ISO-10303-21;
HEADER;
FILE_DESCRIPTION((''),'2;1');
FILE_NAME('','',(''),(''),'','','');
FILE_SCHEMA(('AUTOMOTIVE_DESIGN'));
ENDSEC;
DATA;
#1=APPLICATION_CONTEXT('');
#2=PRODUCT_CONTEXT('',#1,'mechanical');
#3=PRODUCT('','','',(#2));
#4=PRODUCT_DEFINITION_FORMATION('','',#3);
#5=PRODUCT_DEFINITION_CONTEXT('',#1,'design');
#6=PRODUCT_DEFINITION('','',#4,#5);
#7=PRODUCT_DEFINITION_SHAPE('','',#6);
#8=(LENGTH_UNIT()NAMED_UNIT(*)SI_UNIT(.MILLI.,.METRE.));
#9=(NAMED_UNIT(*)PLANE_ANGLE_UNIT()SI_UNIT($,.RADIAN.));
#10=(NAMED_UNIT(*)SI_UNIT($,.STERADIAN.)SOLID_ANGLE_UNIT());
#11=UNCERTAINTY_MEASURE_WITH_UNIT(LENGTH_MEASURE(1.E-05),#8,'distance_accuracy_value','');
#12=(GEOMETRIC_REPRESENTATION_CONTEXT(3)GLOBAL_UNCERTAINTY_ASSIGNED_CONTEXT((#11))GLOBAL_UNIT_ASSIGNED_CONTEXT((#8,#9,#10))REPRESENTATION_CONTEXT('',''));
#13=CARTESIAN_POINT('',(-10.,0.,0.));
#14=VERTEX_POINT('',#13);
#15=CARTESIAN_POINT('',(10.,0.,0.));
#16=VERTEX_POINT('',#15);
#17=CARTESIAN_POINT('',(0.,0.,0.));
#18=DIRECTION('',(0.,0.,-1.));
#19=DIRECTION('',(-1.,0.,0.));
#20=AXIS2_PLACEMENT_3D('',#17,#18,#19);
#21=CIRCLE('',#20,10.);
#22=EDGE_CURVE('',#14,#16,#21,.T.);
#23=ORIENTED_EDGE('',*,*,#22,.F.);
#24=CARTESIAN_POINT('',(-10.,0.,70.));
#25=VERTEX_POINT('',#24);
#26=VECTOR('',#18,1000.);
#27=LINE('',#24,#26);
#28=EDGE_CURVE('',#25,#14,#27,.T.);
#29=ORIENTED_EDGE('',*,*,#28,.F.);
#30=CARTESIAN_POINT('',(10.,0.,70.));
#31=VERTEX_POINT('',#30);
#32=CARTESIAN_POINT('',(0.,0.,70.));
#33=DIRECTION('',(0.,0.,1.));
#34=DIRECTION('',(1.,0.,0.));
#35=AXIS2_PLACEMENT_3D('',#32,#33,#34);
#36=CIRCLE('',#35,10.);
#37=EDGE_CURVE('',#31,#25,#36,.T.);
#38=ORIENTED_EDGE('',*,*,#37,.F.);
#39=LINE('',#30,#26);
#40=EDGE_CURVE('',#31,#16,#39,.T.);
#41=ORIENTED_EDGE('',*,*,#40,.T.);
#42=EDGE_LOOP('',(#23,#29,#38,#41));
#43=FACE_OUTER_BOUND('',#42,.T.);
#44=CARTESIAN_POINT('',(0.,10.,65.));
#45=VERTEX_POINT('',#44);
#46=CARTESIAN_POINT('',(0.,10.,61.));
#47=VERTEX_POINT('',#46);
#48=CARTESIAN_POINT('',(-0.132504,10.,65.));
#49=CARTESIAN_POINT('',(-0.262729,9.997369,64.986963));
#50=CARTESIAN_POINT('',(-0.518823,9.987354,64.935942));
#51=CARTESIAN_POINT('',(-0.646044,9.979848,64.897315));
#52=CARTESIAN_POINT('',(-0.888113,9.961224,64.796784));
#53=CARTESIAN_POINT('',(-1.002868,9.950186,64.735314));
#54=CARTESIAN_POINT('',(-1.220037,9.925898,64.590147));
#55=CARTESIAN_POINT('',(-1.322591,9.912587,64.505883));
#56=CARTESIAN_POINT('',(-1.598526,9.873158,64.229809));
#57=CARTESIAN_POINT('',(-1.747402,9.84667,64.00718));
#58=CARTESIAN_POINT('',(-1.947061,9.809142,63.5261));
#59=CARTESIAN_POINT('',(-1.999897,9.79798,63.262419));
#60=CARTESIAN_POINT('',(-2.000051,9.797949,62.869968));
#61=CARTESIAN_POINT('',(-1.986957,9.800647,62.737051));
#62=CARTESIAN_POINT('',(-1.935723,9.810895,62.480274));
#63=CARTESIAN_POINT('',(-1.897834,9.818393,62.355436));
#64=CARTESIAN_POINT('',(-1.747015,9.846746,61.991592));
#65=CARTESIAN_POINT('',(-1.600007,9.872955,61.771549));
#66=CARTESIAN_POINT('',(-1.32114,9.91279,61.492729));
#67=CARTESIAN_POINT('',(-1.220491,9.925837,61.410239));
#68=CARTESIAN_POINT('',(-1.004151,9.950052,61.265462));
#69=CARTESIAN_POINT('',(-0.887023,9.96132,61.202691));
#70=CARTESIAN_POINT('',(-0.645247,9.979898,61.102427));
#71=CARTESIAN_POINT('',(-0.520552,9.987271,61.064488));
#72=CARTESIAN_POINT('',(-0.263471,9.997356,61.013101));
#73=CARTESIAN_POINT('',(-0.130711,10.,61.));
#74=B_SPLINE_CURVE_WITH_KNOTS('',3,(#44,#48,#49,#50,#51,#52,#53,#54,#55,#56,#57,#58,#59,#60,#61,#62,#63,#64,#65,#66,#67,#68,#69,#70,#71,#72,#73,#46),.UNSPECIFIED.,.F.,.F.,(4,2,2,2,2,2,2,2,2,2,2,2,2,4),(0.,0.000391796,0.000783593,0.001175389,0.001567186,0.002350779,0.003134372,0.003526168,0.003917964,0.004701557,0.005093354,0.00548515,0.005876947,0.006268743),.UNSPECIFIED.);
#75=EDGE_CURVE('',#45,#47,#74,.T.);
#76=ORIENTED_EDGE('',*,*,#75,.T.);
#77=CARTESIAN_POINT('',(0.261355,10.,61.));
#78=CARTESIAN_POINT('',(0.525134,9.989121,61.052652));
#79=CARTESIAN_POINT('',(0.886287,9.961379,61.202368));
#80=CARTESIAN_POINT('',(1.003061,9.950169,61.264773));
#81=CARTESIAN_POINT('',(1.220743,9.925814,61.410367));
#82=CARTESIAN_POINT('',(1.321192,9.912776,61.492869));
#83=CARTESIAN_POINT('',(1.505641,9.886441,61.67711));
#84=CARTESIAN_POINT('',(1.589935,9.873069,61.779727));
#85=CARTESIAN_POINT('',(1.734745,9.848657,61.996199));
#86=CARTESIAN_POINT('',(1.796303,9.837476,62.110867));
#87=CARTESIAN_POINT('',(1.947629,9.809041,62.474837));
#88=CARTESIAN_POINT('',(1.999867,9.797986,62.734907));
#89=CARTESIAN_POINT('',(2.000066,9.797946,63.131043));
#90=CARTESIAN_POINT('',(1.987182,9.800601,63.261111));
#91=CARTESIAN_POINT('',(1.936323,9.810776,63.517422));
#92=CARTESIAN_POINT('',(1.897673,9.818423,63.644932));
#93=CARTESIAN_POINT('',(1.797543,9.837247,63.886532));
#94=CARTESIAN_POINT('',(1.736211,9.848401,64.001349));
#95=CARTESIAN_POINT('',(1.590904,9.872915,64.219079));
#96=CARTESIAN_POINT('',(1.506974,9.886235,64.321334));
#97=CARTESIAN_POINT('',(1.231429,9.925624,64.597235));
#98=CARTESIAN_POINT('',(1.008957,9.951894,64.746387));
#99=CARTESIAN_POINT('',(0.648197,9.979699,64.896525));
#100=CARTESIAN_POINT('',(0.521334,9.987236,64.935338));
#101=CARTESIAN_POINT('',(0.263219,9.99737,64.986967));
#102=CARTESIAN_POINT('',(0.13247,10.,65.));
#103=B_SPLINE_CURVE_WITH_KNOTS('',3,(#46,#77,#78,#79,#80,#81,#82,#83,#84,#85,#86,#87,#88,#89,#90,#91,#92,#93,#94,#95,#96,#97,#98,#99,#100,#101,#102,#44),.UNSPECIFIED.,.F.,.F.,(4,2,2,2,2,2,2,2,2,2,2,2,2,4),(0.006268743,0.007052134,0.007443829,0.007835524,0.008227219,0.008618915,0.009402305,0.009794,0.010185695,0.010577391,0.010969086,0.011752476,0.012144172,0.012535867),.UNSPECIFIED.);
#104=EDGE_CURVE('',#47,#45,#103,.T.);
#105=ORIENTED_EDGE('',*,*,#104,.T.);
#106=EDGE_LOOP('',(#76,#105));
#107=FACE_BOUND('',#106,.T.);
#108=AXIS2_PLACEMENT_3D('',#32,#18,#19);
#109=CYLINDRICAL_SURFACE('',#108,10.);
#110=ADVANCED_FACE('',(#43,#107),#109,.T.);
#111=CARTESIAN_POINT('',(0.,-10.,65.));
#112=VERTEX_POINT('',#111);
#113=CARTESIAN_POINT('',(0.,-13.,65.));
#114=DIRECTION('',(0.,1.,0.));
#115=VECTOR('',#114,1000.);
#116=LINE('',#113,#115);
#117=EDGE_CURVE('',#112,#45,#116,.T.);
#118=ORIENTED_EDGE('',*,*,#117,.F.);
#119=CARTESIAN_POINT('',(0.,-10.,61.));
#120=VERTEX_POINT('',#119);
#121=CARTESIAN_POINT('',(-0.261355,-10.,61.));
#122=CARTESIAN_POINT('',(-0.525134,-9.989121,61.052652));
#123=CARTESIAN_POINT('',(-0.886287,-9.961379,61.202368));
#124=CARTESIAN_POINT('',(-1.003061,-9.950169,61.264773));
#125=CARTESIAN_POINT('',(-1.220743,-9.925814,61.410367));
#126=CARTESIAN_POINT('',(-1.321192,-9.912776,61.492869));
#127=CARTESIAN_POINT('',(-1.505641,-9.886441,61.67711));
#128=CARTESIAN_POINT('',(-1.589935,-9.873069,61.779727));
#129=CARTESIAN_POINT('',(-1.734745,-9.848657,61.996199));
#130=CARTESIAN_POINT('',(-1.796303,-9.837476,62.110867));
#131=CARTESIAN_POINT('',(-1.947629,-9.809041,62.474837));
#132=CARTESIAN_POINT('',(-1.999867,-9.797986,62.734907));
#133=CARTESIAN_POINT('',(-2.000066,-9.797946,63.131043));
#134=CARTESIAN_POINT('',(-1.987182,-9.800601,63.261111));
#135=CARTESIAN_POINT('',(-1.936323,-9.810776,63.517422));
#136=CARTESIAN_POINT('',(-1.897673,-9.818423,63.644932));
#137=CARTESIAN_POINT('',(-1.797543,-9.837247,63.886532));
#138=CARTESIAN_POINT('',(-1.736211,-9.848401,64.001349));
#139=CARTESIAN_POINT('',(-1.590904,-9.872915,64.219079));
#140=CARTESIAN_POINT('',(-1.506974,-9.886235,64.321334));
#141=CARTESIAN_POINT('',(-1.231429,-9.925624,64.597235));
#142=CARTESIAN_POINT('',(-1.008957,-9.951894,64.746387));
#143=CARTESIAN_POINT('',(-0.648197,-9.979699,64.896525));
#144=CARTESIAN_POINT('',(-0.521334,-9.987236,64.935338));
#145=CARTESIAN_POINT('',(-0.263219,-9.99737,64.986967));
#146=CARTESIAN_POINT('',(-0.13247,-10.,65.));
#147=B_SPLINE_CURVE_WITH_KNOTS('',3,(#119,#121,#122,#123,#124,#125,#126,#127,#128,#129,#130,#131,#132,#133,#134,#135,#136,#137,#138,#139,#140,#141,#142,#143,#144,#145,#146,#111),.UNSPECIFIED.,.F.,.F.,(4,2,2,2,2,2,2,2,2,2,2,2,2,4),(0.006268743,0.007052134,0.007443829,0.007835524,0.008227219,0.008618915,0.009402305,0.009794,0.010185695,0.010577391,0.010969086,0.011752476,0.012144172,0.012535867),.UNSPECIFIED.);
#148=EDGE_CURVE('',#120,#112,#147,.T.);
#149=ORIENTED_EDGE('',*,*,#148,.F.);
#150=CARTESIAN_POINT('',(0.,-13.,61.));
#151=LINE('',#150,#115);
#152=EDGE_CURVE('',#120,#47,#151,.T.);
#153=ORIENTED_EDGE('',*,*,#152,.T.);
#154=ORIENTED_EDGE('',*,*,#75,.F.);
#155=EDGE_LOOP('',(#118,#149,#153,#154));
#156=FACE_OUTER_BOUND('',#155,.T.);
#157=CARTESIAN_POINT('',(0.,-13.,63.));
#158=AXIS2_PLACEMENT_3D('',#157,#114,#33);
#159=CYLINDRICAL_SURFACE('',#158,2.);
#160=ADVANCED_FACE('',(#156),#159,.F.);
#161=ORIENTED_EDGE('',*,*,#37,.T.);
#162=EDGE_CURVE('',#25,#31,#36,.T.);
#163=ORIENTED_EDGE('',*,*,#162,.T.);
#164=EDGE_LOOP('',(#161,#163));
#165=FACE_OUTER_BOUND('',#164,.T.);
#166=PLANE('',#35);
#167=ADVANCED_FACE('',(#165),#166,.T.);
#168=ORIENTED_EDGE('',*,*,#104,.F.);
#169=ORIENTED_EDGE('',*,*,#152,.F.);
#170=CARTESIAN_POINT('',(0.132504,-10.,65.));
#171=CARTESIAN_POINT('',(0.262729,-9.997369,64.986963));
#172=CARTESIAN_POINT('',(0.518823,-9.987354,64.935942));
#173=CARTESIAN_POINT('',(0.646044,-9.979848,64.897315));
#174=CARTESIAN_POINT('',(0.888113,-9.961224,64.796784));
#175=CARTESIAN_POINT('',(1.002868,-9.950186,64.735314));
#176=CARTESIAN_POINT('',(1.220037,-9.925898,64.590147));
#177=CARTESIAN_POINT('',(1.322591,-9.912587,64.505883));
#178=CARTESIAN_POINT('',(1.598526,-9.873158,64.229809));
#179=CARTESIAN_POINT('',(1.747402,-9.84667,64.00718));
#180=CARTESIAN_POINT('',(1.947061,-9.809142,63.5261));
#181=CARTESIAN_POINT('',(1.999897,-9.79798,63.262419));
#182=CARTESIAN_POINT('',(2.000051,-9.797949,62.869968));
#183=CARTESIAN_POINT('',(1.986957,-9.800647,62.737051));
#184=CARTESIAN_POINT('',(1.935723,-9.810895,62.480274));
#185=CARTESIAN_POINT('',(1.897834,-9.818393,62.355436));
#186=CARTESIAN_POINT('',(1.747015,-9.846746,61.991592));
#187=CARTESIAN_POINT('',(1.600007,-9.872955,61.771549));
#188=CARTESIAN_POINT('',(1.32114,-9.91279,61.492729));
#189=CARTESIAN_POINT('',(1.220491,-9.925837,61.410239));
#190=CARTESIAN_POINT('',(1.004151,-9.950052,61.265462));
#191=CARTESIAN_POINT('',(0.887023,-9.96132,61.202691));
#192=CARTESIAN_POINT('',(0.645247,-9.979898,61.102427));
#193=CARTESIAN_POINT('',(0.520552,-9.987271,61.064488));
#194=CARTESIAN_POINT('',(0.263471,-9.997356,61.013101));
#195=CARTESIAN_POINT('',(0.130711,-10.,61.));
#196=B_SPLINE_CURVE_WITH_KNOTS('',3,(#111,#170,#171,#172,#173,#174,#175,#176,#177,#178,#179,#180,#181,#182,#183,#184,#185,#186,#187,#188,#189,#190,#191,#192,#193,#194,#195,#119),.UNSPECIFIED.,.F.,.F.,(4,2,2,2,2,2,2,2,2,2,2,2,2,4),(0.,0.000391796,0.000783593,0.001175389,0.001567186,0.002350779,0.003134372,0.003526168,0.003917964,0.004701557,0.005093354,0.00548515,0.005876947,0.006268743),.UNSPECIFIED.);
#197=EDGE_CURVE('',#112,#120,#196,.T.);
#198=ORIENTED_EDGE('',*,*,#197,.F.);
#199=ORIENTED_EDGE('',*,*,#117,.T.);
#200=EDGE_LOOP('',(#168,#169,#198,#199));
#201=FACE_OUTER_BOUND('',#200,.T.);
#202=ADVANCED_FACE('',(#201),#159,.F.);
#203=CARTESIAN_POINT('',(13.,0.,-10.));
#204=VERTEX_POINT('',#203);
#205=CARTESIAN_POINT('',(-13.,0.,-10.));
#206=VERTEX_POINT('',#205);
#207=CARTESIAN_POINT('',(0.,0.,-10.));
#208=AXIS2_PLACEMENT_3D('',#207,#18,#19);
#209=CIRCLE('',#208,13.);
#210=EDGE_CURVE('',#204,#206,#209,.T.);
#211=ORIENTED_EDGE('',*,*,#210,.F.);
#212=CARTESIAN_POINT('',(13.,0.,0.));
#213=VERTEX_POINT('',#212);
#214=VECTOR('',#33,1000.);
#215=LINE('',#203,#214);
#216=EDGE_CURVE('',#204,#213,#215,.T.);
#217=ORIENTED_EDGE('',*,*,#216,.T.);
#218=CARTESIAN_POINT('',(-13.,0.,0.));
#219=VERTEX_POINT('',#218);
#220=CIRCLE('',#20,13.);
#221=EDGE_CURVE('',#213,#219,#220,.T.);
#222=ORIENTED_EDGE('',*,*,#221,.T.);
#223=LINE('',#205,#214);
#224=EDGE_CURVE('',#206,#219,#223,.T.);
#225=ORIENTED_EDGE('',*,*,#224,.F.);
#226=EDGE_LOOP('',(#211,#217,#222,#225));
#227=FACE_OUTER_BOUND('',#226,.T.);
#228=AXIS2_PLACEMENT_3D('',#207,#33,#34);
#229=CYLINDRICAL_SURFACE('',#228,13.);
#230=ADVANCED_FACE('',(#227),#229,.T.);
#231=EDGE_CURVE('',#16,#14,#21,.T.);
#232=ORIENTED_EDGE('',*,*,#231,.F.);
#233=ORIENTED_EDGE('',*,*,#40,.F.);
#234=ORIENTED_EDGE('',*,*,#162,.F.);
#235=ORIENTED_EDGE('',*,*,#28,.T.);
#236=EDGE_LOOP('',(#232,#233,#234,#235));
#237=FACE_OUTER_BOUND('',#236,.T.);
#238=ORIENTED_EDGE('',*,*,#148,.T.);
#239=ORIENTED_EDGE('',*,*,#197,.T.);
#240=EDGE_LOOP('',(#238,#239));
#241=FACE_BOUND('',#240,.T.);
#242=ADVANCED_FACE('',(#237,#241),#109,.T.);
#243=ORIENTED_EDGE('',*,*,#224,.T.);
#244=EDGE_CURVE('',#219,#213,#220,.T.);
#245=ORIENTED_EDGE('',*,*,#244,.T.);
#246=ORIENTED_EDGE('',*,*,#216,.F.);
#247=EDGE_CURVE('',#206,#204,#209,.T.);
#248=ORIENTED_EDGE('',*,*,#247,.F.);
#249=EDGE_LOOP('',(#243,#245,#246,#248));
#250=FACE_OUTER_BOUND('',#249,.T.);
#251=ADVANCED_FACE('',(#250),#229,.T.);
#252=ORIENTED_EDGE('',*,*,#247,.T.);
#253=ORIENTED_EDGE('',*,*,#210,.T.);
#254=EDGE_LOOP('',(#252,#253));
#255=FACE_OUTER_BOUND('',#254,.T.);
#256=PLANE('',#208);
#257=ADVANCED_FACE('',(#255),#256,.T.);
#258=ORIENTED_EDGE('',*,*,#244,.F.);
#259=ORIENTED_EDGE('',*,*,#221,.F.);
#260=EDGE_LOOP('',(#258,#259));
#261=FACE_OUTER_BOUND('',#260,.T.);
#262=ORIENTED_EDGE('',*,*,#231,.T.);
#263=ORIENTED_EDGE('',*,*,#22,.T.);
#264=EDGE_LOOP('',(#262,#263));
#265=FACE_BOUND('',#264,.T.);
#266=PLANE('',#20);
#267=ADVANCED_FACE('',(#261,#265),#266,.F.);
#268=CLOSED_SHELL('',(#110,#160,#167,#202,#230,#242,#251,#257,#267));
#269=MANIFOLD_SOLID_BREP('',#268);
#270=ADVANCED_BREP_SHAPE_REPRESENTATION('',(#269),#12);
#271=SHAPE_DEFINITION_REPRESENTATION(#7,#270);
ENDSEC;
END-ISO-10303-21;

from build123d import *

# Parameters (mm, degrees)
SKETCH1_R               = 10
BOSS_EXTRUDE1_DEPTH     = 70
SKETCH2_R               = 13
BOSS_EXTRUDE2_DEPTH     = 10
CUT_EXTRUDE1_DEPTH      = 73.374028491
CUT_EXTRUDE1_DEPTH_BACK = 73.374028491
SKETCH3_R               = 2


with BuildPart() as part:
    # Sketch1 → Boss-Extrude1 (new body)
    with BuildSketch(Plane.XY):
        Circle(SKETCH1_R)
    extrude(amount=BOSS_EXTRUDE1_DEPTH)

    # Sketch2 → Boss-Extrude2 (add)
    with BuildSketch(Plane(origin=(0, 0, 0), x_dir=(-1, 0, 0), z_dir=(0, 0, -1))):
        Circle(SKETCH2_R)
    extrude(amount=BOSS_EXTRUDE2_DEPTH)

    # Sketch3 → Cut-Extrude1 (cut, two sides: drawn at the far end of the back side and taken through both)
    with BuildSketch(Plane(origin=(0, 0, 0), x_dir=(1, 0, 0), z_dir=(0, 1, 0)).offset(-CUT_EXTRUDE1_DEPTH_BACK)):
        with Locations(Location((0, -63, 0), (0, 0, 270))):
            Circle(SKETCH3_R)
    extrude(amount=CUT_EXTRUDE1_DEPTH + CUT_EXTRUDE1_DEPTH_BACK, mode=Mode.SUBTRACT)


solid = part.part
